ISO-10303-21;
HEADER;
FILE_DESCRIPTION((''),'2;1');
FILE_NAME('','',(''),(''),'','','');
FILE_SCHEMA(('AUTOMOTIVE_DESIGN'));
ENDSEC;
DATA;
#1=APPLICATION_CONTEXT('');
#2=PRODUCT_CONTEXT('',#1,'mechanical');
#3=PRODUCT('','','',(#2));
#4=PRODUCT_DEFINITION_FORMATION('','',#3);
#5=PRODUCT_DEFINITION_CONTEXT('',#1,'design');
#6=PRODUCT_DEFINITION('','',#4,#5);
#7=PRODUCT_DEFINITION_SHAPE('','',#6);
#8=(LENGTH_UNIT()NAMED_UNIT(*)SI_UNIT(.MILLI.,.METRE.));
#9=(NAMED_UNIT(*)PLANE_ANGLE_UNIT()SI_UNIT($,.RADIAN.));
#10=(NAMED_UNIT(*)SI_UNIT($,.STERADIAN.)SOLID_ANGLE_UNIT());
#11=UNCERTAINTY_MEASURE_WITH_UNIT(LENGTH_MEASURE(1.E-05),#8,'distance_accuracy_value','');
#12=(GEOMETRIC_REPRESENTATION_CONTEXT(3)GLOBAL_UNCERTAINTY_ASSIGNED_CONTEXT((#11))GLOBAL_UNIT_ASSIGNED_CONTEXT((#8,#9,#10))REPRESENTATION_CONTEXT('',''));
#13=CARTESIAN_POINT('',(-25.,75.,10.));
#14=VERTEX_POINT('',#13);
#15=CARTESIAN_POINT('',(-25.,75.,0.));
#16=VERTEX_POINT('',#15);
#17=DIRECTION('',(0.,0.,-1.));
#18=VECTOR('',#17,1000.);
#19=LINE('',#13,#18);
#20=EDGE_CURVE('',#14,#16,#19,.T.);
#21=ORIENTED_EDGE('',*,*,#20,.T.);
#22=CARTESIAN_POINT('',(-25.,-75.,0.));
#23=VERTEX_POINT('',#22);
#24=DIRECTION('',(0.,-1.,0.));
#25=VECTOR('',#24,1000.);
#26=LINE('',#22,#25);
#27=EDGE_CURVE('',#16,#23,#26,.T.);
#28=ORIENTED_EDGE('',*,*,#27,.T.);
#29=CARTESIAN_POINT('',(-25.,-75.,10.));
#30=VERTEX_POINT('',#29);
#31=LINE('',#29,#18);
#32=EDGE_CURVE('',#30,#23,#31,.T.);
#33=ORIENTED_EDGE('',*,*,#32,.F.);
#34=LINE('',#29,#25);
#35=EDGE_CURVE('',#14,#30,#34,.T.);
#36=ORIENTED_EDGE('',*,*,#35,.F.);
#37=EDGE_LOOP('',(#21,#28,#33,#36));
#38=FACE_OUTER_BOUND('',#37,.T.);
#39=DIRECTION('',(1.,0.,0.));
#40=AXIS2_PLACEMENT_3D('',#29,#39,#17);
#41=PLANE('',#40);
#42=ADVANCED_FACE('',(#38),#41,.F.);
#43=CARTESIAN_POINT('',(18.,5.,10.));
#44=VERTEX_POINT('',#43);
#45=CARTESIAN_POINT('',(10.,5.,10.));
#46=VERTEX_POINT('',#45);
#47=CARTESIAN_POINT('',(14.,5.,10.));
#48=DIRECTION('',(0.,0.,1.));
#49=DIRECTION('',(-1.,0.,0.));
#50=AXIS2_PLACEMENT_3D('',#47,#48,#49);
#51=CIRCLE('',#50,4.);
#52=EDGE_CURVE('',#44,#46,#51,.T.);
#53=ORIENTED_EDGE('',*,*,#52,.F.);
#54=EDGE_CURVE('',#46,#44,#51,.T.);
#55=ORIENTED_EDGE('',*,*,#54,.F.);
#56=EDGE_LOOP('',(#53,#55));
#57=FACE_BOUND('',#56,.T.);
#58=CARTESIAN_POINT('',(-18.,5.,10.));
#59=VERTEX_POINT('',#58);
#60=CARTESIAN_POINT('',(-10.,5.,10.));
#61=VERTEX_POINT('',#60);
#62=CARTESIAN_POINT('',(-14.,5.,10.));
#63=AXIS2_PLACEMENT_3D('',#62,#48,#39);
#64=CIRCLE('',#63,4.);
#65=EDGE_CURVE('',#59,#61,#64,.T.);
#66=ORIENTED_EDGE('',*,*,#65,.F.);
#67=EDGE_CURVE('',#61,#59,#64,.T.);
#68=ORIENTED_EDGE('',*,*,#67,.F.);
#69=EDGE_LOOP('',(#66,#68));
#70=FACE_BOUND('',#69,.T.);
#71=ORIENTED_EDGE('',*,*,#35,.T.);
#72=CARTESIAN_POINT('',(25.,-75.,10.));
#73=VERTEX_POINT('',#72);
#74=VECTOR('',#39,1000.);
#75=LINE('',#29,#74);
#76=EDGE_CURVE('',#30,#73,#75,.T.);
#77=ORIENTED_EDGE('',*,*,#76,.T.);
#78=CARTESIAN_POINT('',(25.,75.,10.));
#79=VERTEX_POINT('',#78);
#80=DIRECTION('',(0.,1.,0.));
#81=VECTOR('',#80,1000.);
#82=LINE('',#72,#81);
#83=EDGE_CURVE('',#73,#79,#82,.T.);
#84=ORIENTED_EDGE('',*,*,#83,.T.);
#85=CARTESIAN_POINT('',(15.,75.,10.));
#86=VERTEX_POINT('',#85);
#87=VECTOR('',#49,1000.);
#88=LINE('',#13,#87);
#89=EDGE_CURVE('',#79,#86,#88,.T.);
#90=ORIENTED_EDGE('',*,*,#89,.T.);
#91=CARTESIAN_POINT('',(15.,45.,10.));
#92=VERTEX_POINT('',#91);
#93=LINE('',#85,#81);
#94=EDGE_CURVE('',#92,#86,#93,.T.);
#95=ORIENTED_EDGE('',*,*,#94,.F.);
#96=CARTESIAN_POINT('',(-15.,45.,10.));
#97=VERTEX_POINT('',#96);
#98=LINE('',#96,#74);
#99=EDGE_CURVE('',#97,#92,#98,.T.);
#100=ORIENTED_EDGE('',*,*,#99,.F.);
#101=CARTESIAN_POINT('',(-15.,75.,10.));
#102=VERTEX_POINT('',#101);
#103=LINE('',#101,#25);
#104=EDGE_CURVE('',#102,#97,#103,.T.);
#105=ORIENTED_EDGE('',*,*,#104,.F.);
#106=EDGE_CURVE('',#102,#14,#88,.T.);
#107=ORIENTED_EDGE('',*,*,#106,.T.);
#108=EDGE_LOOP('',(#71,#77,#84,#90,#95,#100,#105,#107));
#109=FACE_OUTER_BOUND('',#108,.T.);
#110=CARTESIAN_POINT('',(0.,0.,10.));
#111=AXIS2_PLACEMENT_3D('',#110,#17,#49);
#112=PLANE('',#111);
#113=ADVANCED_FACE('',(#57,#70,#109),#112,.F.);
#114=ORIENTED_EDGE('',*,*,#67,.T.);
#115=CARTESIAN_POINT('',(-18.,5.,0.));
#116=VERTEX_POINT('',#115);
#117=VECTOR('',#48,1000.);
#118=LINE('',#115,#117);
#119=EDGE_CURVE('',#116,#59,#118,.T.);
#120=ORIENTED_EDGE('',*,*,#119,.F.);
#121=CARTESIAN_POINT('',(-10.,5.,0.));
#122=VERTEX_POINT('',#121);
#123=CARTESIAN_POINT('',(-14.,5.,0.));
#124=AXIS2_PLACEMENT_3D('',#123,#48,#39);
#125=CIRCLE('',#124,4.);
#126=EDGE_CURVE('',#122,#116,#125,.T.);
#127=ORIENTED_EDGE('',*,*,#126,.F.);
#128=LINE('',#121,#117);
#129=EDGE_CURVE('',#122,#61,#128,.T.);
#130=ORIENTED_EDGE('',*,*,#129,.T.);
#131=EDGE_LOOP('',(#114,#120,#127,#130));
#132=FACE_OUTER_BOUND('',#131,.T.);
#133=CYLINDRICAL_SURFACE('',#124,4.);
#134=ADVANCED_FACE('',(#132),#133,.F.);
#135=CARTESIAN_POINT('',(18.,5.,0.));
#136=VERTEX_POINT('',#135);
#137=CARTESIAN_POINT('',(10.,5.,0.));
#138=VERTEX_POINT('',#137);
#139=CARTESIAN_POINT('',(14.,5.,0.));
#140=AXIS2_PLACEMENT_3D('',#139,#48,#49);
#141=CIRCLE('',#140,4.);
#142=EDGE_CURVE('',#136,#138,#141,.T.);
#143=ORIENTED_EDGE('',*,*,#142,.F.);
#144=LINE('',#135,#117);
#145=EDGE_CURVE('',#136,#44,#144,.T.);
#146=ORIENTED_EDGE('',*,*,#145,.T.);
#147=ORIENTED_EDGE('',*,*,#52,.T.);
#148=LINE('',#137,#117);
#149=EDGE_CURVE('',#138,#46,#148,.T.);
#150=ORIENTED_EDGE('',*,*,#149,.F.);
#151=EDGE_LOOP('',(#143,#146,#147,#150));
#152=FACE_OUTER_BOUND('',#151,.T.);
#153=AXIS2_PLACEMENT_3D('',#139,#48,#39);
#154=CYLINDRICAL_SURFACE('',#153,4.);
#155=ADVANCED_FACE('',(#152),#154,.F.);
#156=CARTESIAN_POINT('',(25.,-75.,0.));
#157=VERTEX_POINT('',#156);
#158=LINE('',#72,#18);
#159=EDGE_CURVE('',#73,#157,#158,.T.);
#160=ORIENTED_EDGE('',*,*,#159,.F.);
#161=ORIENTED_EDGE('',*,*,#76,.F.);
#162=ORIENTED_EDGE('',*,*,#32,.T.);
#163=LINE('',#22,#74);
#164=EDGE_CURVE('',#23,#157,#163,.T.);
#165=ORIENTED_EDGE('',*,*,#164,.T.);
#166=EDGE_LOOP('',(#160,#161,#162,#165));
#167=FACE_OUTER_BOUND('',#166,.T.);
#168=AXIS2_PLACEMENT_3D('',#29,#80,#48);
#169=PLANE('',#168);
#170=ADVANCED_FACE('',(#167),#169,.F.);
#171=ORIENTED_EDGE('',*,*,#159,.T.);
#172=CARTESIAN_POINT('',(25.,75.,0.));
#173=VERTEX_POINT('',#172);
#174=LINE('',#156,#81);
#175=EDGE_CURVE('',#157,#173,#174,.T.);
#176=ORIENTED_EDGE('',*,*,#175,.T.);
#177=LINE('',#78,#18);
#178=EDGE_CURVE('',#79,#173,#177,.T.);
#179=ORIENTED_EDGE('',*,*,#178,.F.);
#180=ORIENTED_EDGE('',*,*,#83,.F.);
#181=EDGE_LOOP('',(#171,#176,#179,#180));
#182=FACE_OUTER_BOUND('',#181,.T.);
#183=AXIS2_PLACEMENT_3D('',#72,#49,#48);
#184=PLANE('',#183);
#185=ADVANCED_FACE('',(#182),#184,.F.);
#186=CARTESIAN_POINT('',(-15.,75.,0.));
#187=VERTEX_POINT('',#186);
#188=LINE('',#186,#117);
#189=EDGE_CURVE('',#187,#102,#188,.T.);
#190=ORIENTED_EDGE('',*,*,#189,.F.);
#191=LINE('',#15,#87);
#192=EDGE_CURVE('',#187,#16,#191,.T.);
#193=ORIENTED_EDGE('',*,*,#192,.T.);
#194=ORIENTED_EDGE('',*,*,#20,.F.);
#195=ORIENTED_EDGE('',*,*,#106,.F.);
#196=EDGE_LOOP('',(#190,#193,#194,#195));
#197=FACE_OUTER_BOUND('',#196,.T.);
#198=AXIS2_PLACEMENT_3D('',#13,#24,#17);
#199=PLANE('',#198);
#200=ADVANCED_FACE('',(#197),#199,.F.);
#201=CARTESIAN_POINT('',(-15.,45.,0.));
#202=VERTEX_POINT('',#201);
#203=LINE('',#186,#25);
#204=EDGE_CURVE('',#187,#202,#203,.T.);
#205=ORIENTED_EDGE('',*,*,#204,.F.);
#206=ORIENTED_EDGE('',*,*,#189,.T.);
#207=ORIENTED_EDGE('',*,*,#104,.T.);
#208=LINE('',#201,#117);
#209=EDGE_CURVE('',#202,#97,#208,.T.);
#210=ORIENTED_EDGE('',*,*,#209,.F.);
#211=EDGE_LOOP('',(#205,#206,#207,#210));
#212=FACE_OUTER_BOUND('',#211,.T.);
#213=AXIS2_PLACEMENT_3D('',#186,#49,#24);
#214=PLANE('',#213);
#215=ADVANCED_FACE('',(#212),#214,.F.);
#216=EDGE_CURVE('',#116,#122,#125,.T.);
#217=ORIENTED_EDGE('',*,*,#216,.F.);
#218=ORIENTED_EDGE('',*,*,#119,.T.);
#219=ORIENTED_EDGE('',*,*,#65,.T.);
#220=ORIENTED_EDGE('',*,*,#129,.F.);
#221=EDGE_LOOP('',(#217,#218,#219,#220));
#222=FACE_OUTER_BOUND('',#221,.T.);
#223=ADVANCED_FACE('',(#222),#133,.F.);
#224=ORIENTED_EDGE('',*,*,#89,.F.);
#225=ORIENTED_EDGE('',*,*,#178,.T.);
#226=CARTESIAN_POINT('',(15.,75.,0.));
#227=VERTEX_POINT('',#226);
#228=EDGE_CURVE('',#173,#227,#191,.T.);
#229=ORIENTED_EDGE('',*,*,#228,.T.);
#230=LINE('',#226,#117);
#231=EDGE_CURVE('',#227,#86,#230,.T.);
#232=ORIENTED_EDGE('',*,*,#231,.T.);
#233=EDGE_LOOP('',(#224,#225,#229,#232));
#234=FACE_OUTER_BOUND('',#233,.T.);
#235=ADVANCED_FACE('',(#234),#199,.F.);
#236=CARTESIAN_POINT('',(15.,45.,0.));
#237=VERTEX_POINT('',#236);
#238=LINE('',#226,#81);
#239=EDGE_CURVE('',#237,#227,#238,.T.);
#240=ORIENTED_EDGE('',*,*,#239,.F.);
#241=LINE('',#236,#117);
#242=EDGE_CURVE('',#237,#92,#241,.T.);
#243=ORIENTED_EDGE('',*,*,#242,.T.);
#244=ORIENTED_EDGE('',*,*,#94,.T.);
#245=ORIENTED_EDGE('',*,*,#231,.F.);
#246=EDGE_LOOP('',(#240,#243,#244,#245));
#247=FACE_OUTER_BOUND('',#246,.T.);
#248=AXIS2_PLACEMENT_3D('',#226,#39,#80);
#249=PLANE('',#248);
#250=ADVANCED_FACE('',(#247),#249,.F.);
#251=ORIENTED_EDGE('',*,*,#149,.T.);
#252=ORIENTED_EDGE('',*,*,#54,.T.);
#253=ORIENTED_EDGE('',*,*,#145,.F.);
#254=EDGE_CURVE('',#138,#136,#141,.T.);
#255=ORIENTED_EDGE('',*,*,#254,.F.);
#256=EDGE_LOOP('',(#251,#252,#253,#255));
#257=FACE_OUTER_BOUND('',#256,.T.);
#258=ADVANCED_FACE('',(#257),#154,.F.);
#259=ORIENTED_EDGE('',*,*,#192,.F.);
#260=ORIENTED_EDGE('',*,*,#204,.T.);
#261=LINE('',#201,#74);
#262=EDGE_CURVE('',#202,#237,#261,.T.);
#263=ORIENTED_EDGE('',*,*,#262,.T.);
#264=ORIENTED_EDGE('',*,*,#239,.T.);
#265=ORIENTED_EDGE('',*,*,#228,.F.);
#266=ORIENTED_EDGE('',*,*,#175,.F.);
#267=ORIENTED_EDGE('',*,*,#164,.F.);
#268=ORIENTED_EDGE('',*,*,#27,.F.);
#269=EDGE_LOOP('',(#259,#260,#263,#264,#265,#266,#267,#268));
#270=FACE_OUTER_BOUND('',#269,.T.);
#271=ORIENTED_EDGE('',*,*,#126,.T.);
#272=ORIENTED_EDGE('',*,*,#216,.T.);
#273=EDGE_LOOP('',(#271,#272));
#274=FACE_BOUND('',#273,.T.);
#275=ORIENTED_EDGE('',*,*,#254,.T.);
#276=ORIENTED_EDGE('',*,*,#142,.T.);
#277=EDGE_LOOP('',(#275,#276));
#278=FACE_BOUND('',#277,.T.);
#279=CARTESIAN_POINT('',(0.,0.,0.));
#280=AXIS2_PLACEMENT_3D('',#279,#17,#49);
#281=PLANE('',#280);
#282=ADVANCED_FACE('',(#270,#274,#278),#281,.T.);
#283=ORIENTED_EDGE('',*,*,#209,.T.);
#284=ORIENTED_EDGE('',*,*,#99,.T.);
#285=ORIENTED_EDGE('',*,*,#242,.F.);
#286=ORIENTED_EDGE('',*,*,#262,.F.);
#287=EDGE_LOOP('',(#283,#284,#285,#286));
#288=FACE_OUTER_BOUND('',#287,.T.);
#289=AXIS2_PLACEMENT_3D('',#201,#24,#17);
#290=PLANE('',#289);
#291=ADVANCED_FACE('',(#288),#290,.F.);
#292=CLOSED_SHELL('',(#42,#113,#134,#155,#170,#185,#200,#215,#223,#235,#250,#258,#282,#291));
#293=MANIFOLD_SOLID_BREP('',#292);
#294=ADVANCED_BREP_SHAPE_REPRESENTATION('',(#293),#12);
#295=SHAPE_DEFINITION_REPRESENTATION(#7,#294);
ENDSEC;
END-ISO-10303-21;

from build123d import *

# Parameters (mm, degrees)
SKETCH1_W           = 50
SKETCH1_H           = 150
BOSS_EXTRUDE1_DEPTH = 10
SKETCH2_W           = 30
SKETCH2_H           = 30
CUT_EXTRUDE1_DEPTH  = 10
SKETCH3_R           = 4
CUT_EXTRUDE2_DEPTH  = 80.686887253


with BuildPart() as part:
    # Sketch1 → Boss-Extrude1 (new body)
    with BuildSketch(Plane.XY):
        Rectangle(SKETCH1_W, SKETCH1_H)
    extrude(amount=BOSS_EXTRUDE1_DEPTH)

    # Sketch2 → Cut-Extrude1 (cut)
    with BuildSketch(Plane.XY.offset(10)):
        with Locations((0, 60)):
            Rectangle(SKETCH2_W, SKETCH2_H)
    extrude(amount=-CUT_EXTRUDE1_DEPTH, mode=Mode.SUBTRACT)

    # Sketch3 → Cut-Extrude2 (cut, through all)
    with BuildSketch(Plane.XY.offset(10)):
        with Locations((-14, 5)):
            Circle(SKETCH3_R)
        with Locations(Location((14, 5, 0), (0, 0, 180))):
            Circle(SKETCH3_R)
    extrude(amount=-CUT_EXTRUDE2_DEPTH, mode=Mode.SUBTRACT)


solid = part.part
